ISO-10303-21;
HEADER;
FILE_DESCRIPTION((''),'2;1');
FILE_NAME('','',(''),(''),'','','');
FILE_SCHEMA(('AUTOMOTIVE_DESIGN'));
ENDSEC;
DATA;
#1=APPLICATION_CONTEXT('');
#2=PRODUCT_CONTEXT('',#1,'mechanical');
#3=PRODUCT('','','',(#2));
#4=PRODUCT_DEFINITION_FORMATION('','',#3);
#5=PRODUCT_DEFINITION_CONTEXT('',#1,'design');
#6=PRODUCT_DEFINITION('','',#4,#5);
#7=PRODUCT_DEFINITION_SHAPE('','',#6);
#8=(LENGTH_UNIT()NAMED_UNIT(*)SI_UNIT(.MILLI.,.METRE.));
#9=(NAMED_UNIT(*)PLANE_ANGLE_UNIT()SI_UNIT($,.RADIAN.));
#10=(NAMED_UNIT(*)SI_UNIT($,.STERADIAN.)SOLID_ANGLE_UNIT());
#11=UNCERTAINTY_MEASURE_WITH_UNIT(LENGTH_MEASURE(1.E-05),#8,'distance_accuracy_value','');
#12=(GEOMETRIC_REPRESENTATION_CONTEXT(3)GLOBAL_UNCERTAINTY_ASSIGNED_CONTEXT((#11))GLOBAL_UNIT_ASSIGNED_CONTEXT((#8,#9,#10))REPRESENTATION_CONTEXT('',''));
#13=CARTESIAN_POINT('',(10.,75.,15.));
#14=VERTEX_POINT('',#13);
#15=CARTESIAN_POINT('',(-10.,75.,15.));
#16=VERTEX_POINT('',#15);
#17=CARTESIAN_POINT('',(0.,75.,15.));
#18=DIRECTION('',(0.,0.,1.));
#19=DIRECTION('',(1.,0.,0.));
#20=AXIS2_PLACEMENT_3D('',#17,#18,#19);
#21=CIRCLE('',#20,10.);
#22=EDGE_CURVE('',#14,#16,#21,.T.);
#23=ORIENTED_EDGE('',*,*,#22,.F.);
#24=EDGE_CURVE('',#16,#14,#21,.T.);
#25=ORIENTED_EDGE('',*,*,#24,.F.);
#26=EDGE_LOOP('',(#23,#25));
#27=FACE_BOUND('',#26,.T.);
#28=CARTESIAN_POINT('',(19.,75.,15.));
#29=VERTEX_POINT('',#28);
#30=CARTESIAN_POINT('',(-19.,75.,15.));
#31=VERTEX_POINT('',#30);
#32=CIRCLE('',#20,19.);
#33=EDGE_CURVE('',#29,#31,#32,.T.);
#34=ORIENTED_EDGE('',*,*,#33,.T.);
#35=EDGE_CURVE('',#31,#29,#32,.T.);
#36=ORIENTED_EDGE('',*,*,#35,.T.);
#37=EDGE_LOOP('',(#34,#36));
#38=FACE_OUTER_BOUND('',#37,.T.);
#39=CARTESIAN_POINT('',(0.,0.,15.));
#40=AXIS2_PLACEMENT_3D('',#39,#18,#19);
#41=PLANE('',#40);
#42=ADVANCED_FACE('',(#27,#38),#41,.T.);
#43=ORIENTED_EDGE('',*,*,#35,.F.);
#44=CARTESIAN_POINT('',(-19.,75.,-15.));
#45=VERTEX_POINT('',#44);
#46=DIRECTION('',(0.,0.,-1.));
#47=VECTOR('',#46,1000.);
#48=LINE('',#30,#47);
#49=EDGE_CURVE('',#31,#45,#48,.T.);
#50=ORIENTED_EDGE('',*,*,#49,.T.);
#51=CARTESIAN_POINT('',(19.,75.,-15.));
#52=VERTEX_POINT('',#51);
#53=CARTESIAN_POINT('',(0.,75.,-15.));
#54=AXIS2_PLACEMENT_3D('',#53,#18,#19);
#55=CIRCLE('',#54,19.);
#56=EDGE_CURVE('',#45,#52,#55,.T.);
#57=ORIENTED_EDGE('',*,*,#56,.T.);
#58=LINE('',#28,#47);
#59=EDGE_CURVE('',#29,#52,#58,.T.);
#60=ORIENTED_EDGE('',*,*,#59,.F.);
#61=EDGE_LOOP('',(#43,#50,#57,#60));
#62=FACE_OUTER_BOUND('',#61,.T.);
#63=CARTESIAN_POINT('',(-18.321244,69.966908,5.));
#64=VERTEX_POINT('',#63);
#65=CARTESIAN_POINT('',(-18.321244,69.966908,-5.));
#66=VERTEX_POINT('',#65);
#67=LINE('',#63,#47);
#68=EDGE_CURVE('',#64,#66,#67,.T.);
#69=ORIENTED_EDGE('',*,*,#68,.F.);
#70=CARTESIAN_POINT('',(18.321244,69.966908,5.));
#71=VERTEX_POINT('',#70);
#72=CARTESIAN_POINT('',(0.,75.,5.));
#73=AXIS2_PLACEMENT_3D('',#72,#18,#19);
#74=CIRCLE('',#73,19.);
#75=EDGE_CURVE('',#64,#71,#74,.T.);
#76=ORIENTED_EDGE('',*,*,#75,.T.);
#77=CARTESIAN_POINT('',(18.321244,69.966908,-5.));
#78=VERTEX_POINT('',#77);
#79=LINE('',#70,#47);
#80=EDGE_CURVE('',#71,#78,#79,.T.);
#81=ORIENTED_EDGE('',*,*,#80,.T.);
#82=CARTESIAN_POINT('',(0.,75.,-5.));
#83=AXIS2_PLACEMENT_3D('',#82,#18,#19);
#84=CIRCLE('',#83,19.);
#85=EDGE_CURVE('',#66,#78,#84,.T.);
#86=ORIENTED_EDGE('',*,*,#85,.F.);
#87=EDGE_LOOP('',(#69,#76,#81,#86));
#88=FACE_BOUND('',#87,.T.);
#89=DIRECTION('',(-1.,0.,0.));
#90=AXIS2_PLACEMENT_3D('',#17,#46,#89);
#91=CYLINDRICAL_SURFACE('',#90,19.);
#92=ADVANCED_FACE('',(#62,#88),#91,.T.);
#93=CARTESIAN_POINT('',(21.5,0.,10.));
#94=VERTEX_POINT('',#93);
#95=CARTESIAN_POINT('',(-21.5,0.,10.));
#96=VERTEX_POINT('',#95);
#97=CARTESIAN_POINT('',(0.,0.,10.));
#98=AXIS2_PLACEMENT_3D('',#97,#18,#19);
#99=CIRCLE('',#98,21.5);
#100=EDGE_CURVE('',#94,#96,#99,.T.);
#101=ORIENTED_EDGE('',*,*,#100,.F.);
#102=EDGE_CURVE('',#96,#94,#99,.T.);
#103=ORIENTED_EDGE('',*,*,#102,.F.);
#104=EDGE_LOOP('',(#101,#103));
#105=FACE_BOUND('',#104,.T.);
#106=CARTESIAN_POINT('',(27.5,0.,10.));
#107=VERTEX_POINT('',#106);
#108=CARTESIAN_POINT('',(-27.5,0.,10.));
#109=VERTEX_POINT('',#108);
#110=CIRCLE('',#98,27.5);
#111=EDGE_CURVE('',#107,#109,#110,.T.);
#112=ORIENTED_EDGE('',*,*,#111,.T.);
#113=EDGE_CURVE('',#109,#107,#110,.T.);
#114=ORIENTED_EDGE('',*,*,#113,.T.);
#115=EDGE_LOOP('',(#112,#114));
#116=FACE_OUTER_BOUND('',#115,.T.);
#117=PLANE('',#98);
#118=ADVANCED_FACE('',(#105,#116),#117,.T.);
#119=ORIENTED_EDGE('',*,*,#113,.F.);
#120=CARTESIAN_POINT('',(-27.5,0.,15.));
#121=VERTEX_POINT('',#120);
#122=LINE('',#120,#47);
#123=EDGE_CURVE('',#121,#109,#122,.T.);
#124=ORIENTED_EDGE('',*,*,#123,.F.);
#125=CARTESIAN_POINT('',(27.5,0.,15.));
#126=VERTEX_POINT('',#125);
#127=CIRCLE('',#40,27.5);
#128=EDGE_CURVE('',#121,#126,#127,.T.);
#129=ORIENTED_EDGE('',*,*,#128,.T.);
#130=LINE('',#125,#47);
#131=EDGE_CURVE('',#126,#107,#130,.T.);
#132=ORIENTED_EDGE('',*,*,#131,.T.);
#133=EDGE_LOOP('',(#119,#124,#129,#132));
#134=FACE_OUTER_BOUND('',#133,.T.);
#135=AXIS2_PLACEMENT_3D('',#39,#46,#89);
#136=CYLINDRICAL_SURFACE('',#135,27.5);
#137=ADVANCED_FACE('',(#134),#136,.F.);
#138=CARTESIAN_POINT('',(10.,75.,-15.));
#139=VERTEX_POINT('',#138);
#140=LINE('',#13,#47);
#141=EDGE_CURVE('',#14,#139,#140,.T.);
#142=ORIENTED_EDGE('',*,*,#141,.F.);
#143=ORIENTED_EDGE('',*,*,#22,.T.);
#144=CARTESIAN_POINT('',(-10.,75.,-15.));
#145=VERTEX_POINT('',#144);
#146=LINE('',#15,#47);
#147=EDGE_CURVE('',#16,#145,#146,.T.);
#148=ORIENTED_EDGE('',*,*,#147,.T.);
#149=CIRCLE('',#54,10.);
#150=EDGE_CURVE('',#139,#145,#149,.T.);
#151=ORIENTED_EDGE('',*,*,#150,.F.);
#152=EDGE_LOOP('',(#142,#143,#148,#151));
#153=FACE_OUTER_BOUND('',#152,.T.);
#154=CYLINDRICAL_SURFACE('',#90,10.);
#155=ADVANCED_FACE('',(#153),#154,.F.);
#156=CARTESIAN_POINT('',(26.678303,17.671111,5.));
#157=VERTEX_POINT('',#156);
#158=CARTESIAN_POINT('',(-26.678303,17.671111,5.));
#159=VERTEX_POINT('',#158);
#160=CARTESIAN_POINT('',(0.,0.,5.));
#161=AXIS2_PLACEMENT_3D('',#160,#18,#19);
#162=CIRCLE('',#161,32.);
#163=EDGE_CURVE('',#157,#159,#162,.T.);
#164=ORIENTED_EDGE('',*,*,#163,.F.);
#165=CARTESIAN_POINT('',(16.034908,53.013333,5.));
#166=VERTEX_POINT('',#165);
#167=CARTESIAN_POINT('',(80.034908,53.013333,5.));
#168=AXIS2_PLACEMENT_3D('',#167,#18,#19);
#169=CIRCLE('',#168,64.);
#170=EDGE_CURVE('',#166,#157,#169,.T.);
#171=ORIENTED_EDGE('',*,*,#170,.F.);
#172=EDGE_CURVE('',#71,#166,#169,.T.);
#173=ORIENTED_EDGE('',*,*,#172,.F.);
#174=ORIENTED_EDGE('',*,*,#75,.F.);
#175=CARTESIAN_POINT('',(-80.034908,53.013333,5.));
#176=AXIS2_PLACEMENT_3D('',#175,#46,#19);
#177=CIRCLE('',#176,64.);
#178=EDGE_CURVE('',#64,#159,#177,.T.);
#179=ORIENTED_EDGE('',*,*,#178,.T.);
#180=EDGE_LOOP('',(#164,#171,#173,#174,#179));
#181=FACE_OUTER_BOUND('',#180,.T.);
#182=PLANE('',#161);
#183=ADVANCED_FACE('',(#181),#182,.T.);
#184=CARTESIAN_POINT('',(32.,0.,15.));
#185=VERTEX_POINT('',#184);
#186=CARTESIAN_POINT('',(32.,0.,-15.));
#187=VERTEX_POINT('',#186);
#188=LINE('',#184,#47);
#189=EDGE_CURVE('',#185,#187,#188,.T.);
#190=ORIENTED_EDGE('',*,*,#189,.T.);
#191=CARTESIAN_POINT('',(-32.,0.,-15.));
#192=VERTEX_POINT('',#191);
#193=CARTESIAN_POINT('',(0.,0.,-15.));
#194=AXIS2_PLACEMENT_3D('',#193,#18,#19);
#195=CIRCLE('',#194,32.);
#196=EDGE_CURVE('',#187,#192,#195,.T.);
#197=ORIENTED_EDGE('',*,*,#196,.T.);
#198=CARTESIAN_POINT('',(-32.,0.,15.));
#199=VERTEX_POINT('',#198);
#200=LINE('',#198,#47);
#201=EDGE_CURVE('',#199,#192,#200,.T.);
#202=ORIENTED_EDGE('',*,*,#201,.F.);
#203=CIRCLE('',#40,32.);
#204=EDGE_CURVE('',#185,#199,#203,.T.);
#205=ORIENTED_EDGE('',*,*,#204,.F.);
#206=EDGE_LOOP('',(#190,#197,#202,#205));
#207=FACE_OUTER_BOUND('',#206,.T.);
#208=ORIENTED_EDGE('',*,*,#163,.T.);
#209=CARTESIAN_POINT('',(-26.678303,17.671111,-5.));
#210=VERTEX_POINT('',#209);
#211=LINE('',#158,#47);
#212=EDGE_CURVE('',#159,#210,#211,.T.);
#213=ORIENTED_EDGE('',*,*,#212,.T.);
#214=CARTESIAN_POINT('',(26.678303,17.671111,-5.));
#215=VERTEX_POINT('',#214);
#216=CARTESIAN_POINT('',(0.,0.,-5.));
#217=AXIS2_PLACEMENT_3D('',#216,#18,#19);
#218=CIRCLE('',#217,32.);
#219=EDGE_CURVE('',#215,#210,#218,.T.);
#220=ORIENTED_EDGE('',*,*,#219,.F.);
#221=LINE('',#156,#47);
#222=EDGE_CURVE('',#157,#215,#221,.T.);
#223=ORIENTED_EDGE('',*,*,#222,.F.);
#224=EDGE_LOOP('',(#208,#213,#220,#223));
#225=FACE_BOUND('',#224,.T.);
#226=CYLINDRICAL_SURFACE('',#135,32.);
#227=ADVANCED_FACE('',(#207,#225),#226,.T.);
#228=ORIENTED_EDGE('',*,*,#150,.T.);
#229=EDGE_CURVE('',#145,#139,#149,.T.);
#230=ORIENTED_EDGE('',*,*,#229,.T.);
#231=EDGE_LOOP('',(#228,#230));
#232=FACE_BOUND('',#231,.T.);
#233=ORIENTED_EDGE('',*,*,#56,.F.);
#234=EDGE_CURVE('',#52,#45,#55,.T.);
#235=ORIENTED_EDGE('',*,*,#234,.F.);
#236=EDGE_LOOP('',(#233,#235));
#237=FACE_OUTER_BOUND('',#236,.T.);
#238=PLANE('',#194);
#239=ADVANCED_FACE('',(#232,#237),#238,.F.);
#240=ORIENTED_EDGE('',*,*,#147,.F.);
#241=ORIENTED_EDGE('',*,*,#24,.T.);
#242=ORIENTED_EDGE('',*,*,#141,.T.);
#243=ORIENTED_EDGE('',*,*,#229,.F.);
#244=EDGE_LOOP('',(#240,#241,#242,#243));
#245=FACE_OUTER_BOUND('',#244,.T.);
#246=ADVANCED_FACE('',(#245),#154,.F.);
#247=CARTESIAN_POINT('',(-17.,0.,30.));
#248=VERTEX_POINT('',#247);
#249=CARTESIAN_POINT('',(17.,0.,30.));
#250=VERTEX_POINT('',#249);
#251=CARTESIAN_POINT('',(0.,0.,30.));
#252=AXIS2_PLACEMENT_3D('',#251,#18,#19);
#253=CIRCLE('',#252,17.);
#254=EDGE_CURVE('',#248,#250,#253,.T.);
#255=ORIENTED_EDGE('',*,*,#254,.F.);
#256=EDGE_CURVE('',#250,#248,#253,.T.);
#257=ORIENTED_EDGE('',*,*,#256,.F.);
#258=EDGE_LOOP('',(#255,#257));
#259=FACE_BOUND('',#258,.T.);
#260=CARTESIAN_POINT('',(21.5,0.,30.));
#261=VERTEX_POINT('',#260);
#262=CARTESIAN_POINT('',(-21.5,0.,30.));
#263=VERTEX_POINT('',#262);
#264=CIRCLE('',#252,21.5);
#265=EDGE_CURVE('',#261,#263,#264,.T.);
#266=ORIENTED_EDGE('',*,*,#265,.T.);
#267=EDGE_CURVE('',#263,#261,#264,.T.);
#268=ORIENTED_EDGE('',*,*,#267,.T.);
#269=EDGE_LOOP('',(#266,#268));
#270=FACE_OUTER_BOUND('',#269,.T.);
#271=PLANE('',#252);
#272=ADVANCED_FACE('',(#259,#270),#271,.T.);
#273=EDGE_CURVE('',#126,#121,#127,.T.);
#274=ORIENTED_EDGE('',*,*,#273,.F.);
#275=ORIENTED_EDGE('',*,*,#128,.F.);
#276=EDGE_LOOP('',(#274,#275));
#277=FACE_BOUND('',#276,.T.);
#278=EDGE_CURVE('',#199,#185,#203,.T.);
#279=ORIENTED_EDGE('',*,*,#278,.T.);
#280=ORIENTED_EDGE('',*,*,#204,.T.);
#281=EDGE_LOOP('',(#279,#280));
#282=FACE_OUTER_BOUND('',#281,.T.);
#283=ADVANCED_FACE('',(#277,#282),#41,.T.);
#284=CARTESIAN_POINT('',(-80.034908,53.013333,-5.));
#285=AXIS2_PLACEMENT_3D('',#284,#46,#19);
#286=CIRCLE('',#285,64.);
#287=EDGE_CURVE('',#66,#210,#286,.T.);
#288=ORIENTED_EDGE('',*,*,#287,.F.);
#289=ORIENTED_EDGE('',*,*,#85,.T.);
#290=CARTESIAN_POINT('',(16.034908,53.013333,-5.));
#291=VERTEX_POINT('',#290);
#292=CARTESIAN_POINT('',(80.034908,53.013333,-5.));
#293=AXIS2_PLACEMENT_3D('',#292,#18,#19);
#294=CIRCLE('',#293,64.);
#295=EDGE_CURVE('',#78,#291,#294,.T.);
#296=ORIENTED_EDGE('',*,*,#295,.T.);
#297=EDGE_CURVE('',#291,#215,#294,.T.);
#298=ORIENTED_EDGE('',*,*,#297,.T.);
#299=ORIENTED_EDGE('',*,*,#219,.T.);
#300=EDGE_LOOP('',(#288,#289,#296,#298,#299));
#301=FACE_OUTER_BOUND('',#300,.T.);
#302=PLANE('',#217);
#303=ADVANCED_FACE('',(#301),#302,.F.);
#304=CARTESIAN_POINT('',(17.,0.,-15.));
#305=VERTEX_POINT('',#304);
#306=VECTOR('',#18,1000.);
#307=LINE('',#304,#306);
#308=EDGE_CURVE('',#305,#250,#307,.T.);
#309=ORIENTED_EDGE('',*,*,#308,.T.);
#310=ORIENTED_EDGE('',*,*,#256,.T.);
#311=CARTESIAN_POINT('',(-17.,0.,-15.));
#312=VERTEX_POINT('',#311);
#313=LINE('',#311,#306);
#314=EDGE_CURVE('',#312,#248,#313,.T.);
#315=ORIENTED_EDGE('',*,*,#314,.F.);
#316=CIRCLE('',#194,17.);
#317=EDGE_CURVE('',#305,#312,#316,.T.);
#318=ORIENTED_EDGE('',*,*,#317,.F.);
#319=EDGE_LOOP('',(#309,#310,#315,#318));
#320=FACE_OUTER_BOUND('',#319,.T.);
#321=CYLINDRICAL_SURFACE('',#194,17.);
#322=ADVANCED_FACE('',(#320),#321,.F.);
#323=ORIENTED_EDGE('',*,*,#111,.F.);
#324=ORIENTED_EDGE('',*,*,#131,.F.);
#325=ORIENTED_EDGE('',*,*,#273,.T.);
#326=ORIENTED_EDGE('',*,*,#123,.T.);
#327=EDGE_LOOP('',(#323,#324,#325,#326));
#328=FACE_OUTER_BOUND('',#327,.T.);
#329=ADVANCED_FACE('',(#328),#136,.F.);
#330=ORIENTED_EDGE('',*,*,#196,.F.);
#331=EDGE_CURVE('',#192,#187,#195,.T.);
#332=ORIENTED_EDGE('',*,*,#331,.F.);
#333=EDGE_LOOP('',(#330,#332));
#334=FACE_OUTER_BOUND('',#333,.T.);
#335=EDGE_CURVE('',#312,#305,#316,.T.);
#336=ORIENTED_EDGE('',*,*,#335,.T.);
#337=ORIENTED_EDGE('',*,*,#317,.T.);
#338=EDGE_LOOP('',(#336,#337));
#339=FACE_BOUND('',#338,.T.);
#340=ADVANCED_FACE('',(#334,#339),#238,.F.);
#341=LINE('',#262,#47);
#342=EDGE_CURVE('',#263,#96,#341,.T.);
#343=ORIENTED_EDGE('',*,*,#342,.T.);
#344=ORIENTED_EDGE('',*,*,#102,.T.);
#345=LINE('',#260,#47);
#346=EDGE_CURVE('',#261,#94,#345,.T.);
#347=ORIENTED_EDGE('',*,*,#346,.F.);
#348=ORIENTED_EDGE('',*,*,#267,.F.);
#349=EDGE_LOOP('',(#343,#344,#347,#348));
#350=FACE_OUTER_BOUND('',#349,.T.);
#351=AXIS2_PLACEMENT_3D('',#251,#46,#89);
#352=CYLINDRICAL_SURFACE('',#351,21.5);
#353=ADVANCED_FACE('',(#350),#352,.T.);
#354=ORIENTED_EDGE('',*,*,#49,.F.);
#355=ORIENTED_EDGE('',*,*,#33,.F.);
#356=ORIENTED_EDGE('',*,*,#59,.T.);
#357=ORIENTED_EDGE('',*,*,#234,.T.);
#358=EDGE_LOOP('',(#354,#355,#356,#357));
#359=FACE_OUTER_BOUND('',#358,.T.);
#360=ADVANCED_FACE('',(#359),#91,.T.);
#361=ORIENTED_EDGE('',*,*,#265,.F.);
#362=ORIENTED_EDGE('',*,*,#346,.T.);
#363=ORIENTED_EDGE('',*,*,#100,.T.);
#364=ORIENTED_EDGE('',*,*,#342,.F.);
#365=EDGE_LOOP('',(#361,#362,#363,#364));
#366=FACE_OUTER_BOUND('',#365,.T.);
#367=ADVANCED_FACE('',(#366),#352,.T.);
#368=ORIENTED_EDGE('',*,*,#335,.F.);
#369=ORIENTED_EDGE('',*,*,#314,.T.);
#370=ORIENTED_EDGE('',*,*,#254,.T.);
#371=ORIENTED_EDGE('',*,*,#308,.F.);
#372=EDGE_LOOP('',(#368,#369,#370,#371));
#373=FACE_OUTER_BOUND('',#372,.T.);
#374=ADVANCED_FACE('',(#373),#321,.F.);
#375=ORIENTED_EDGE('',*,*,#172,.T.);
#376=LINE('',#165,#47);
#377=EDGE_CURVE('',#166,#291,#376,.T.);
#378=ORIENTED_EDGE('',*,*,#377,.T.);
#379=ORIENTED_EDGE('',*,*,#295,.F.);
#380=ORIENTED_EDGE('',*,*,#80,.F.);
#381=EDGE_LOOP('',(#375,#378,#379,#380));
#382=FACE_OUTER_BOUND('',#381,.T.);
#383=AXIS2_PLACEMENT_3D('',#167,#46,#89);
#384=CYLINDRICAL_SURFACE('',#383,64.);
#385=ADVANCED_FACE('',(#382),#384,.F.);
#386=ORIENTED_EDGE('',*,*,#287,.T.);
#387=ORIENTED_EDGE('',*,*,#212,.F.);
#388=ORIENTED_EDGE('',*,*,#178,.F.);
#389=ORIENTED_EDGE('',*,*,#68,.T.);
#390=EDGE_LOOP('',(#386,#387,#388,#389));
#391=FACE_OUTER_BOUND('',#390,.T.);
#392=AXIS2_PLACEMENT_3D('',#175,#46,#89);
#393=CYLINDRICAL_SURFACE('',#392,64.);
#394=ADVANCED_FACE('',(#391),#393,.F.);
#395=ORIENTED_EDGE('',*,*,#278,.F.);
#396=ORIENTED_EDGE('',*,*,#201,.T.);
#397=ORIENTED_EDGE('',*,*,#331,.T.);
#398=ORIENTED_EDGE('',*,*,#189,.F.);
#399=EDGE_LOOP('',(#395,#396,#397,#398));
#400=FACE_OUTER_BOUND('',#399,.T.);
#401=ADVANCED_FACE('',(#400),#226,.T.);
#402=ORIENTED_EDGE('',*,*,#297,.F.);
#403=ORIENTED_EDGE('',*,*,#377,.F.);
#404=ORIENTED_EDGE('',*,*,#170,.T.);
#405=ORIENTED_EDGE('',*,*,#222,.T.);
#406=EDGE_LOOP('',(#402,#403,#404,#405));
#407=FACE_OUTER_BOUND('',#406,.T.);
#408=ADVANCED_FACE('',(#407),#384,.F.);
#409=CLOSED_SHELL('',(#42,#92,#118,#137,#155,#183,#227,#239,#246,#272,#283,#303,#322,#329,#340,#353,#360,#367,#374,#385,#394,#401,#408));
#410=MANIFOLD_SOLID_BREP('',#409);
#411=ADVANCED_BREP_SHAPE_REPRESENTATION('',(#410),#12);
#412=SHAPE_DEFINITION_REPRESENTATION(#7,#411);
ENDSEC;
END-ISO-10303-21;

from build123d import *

# Parameters (mm, degrees)
LEVER_PROFILE_SKETCH_R         = 32
LEVER_PROFILE_SKETCH_R_2       = 27.5
LEVER_BODY_30MM_DEPTH          = 15
LEVER_PROFILE_SKETCH_R_3       = 19
LEVER_PROFILE_SKETCH_R_4       = 10
LEVER_BODY_30MM_2_DEPTH        = 15
WEB_EXTRUDE_10MM_DEPTH         = 5
BIG_END_HUB_10_15MM_DEPTH      = 10
BIG_END_HUB_10_15MM_DEPTH_BACK = 15
SKETCH1_5_R                    = 27.5
SKETCH1_5_R_2                  = 17
BIG_START                      = 10
SKETCH1_6_R                    = 21.5
SKETCH1_6_R_2                  = 17
BIG_END_SLEEVE_20MM_DEPTH      = 20


with BuildPart() as part:
    # Lever Profile Sketch → Lever Body 30mm (new, symmetric)
    with BuildSketch(Plane.XY):
        Circle(LEVER_PROFILE_SKETCH_R)
        Circle(LEVER_PROFILE_SKETCH_R_2, mode=Mode.SUBTRACT)
    extrude(amount=LEVER_BODY_30MM_DEPTH, both=True)



with BuildPart() as body_2:
    # Lever Profile Sketch → Lever Body 30mm 2 (new, symmetric)
    with BuildSketch(Plane.XY):
        with Locations((0, 75)):
            Circle(LEVER_PROFILE_SKETCH_R_3)
        with Locations((0, 75)):
            Circle(LEVER_PROFILE_SKETCH_R_4, mode=Mode.SUBTRACT)
    extrude(amount=LEVER_BODY_30MM_2_DEPTH, both=True)


with BuildPart() as part_1:
    add(part.part)

    add(body_2.part)  # Web Extrude 10mm merges body 2
    # Sketch1_4 → Web Extrude 10mm (add, symmetric)
    with BuildSketch(Plane.XY):
        with BuildLine():
            Line((0, 32), (0, 56))
            ThreePointArc((0, 56), (-11.518924537, 59.889924636), (-18.321243986, 69.966907631))
            ThreePointArc((-18.321243986, 69.966907631), (-16.836772686, 42.914041255), (-26.678302647, 17.671111111))
            ThreePointArc((-26.678302647, 17.671111111), (-15.141407538, 28.191093944), (0, 32))
        make_face()
        with BuildLine():
            ThreePointArc((18.321243986, 69.966907631), (11.518924537, 59.889924636), (0, 56))
            Line((0, 56), (0, 32))
            ThreePointArc((0, 32), (15.141407538, 28.191093944), (26.678302647, 17.671111111))
            ThreePointArc((26.678302647, 17.671111111), (16.836772686, 42.914041255), (18.321243986, 69.966907631))
        make_face()
    extrude(amount=WEB_EXTRUDE_10MM_DEPTH, both=True)

    # Sketch1_5 → Big End Hub 10_15mm (add, two sides: drawn at the far end of the back side and taken through both)
    with BuildSketch(Plane.XY.offset(-BIG_END_HUB_10_15MM_DEPTH_BACK)):
        Circle(SKETCH1_5_R)
        Circle(SKETCH1_5_R_2, mode=Mode.SUBTRACT)
    extrude(amount=BIG_END_HUB_10_15MM_DEPTH + BIG_END_HUB_10_15MM_DEPTH_BACK)

    # Sketch1_6 → Big End Sleeve 20mm (add)
    with BuildSketch(Plane.XY.offset(BIG_START)):
        Circle(SKETCH1_6_R)
        Circle(SKETCH1_6_R_2, mode=Mode.SUBTRACT)
    extrude(amount=BIG_END_SLEEVE_20MM_DEPTH)


solid = part_1.part
